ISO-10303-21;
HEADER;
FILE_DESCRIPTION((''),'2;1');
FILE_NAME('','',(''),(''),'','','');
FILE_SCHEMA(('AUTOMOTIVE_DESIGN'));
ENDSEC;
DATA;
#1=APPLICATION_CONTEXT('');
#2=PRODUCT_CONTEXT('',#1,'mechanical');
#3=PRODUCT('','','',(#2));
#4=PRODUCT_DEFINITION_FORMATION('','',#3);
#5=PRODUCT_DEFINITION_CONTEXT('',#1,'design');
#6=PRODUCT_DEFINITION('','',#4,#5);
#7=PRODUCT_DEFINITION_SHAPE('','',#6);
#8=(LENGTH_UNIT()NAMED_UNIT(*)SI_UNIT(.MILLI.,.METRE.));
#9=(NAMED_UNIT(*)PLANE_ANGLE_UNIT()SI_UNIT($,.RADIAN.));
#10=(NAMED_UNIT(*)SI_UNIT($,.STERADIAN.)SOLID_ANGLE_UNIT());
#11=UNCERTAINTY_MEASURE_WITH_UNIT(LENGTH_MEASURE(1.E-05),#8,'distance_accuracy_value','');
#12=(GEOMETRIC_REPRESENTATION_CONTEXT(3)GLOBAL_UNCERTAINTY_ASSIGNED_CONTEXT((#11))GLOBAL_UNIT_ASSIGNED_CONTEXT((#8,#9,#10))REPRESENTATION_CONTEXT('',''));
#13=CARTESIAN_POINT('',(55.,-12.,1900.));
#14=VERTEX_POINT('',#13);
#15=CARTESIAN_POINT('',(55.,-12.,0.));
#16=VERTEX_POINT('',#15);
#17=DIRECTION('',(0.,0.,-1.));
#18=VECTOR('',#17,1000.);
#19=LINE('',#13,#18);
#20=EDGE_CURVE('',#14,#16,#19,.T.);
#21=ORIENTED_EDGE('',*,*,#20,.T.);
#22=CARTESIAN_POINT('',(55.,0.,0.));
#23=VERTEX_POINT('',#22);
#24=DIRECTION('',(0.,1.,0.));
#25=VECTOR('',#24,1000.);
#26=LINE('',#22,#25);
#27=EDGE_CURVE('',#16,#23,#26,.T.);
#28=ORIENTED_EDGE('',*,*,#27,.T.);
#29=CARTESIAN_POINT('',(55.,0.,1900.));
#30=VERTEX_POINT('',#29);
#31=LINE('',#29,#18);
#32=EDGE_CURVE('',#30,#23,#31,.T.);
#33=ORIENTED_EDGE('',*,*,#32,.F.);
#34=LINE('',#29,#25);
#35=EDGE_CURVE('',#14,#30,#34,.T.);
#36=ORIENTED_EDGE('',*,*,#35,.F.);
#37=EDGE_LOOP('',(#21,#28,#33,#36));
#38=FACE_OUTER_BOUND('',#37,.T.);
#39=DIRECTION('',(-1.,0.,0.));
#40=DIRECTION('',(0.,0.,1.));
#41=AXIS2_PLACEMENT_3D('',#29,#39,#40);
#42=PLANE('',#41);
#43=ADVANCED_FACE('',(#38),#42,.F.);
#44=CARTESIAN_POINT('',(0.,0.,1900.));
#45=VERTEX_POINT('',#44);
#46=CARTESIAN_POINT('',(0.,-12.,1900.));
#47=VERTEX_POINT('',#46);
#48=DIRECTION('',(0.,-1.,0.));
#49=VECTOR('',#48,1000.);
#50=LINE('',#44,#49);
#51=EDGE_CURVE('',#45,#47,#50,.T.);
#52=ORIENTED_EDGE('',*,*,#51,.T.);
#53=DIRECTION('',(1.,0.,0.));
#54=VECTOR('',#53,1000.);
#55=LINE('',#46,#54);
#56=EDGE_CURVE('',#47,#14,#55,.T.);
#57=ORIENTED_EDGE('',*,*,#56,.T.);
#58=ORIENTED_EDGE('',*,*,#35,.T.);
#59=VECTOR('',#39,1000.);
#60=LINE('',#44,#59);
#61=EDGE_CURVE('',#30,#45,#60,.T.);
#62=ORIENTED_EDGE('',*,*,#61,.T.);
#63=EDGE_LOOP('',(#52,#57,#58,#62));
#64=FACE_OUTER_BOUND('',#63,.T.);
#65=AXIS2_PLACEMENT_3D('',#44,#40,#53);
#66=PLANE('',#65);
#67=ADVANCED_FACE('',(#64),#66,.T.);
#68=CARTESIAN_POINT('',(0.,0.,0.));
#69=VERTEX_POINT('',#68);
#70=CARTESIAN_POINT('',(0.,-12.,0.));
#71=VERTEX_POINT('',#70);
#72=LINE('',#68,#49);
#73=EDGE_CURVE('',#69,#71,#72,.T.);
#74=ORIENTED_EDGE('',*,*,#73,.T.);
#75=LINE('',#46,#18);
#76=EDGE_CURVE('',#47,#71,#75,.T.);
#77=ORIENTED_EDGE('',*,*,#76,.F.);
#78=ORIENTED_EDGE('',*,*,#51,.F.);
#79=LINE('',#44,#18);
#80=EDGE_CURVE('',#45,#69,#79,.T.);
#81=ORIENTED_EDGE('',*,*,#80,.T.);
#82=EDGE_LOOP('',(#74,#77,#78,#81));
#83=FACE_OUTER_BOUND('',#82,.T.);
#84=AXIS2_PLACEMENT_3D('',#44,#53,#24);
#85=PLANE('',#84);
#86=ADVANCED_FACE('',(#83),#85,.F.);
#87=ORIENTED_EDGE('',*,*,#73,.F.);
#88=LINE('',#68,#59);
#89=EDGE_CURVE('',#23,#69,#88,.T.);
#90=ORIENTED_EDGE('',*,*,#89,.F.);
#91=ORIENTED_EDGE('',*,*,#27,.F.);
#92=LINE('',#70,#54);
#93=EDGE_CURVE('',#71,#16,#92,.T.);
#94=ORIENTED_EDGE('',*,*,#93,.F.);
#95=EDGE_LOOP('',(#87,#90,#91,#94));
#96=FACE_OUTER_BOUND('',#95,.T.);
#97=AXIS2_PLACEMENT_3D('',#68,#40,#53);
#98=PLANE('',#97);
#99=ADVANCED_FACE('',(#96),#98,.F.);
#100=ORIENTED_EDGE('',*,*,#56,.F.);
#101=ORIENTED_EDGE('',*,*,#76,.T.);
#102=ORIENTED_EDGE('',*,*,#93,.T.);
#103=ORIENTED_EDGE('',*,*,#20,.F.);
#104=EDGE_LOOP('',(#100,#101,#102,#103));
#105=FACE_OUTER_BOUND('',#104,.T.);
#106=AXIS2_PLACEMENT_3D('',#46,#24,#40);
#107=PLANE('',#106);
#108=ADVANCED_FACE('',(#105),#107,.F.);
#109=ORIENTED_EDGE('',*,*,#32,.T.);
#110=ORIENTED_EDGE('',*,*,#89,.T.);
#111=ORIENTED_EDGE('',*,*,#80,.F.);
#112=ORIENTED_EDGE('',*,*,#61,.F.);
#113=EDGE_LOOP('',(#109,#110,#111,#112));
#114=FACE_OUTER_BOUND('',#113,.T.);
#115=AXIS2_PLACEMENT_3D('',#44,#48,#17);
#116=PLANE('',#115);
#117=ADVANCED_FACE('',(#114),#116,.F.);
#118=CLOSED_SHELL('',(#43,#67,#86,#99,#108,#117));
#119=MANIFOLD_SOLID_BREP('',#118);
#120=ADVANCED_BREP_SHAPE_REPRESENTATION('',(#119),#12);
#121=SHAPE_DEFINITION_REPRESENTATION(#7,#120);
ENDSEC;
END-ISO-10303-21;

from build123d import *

# Parameters (mm, degrees)
SKETCH_1_W      = 55
SKETCH_1_H      = 12
EXTRUDE_1_DEPTH = 1900


with BuildPart() as part:
    # 草图1 → 凸台-拉伸1 (new body)
    with BuildSketch(Plane.XY):
        with Locations((27.5, -6)):
            Rectangle(SKETCH_1_W, SKETCH_1_H)
    extrude(amount=EXTRUDE_1_DEPTH)


solid = part.part
